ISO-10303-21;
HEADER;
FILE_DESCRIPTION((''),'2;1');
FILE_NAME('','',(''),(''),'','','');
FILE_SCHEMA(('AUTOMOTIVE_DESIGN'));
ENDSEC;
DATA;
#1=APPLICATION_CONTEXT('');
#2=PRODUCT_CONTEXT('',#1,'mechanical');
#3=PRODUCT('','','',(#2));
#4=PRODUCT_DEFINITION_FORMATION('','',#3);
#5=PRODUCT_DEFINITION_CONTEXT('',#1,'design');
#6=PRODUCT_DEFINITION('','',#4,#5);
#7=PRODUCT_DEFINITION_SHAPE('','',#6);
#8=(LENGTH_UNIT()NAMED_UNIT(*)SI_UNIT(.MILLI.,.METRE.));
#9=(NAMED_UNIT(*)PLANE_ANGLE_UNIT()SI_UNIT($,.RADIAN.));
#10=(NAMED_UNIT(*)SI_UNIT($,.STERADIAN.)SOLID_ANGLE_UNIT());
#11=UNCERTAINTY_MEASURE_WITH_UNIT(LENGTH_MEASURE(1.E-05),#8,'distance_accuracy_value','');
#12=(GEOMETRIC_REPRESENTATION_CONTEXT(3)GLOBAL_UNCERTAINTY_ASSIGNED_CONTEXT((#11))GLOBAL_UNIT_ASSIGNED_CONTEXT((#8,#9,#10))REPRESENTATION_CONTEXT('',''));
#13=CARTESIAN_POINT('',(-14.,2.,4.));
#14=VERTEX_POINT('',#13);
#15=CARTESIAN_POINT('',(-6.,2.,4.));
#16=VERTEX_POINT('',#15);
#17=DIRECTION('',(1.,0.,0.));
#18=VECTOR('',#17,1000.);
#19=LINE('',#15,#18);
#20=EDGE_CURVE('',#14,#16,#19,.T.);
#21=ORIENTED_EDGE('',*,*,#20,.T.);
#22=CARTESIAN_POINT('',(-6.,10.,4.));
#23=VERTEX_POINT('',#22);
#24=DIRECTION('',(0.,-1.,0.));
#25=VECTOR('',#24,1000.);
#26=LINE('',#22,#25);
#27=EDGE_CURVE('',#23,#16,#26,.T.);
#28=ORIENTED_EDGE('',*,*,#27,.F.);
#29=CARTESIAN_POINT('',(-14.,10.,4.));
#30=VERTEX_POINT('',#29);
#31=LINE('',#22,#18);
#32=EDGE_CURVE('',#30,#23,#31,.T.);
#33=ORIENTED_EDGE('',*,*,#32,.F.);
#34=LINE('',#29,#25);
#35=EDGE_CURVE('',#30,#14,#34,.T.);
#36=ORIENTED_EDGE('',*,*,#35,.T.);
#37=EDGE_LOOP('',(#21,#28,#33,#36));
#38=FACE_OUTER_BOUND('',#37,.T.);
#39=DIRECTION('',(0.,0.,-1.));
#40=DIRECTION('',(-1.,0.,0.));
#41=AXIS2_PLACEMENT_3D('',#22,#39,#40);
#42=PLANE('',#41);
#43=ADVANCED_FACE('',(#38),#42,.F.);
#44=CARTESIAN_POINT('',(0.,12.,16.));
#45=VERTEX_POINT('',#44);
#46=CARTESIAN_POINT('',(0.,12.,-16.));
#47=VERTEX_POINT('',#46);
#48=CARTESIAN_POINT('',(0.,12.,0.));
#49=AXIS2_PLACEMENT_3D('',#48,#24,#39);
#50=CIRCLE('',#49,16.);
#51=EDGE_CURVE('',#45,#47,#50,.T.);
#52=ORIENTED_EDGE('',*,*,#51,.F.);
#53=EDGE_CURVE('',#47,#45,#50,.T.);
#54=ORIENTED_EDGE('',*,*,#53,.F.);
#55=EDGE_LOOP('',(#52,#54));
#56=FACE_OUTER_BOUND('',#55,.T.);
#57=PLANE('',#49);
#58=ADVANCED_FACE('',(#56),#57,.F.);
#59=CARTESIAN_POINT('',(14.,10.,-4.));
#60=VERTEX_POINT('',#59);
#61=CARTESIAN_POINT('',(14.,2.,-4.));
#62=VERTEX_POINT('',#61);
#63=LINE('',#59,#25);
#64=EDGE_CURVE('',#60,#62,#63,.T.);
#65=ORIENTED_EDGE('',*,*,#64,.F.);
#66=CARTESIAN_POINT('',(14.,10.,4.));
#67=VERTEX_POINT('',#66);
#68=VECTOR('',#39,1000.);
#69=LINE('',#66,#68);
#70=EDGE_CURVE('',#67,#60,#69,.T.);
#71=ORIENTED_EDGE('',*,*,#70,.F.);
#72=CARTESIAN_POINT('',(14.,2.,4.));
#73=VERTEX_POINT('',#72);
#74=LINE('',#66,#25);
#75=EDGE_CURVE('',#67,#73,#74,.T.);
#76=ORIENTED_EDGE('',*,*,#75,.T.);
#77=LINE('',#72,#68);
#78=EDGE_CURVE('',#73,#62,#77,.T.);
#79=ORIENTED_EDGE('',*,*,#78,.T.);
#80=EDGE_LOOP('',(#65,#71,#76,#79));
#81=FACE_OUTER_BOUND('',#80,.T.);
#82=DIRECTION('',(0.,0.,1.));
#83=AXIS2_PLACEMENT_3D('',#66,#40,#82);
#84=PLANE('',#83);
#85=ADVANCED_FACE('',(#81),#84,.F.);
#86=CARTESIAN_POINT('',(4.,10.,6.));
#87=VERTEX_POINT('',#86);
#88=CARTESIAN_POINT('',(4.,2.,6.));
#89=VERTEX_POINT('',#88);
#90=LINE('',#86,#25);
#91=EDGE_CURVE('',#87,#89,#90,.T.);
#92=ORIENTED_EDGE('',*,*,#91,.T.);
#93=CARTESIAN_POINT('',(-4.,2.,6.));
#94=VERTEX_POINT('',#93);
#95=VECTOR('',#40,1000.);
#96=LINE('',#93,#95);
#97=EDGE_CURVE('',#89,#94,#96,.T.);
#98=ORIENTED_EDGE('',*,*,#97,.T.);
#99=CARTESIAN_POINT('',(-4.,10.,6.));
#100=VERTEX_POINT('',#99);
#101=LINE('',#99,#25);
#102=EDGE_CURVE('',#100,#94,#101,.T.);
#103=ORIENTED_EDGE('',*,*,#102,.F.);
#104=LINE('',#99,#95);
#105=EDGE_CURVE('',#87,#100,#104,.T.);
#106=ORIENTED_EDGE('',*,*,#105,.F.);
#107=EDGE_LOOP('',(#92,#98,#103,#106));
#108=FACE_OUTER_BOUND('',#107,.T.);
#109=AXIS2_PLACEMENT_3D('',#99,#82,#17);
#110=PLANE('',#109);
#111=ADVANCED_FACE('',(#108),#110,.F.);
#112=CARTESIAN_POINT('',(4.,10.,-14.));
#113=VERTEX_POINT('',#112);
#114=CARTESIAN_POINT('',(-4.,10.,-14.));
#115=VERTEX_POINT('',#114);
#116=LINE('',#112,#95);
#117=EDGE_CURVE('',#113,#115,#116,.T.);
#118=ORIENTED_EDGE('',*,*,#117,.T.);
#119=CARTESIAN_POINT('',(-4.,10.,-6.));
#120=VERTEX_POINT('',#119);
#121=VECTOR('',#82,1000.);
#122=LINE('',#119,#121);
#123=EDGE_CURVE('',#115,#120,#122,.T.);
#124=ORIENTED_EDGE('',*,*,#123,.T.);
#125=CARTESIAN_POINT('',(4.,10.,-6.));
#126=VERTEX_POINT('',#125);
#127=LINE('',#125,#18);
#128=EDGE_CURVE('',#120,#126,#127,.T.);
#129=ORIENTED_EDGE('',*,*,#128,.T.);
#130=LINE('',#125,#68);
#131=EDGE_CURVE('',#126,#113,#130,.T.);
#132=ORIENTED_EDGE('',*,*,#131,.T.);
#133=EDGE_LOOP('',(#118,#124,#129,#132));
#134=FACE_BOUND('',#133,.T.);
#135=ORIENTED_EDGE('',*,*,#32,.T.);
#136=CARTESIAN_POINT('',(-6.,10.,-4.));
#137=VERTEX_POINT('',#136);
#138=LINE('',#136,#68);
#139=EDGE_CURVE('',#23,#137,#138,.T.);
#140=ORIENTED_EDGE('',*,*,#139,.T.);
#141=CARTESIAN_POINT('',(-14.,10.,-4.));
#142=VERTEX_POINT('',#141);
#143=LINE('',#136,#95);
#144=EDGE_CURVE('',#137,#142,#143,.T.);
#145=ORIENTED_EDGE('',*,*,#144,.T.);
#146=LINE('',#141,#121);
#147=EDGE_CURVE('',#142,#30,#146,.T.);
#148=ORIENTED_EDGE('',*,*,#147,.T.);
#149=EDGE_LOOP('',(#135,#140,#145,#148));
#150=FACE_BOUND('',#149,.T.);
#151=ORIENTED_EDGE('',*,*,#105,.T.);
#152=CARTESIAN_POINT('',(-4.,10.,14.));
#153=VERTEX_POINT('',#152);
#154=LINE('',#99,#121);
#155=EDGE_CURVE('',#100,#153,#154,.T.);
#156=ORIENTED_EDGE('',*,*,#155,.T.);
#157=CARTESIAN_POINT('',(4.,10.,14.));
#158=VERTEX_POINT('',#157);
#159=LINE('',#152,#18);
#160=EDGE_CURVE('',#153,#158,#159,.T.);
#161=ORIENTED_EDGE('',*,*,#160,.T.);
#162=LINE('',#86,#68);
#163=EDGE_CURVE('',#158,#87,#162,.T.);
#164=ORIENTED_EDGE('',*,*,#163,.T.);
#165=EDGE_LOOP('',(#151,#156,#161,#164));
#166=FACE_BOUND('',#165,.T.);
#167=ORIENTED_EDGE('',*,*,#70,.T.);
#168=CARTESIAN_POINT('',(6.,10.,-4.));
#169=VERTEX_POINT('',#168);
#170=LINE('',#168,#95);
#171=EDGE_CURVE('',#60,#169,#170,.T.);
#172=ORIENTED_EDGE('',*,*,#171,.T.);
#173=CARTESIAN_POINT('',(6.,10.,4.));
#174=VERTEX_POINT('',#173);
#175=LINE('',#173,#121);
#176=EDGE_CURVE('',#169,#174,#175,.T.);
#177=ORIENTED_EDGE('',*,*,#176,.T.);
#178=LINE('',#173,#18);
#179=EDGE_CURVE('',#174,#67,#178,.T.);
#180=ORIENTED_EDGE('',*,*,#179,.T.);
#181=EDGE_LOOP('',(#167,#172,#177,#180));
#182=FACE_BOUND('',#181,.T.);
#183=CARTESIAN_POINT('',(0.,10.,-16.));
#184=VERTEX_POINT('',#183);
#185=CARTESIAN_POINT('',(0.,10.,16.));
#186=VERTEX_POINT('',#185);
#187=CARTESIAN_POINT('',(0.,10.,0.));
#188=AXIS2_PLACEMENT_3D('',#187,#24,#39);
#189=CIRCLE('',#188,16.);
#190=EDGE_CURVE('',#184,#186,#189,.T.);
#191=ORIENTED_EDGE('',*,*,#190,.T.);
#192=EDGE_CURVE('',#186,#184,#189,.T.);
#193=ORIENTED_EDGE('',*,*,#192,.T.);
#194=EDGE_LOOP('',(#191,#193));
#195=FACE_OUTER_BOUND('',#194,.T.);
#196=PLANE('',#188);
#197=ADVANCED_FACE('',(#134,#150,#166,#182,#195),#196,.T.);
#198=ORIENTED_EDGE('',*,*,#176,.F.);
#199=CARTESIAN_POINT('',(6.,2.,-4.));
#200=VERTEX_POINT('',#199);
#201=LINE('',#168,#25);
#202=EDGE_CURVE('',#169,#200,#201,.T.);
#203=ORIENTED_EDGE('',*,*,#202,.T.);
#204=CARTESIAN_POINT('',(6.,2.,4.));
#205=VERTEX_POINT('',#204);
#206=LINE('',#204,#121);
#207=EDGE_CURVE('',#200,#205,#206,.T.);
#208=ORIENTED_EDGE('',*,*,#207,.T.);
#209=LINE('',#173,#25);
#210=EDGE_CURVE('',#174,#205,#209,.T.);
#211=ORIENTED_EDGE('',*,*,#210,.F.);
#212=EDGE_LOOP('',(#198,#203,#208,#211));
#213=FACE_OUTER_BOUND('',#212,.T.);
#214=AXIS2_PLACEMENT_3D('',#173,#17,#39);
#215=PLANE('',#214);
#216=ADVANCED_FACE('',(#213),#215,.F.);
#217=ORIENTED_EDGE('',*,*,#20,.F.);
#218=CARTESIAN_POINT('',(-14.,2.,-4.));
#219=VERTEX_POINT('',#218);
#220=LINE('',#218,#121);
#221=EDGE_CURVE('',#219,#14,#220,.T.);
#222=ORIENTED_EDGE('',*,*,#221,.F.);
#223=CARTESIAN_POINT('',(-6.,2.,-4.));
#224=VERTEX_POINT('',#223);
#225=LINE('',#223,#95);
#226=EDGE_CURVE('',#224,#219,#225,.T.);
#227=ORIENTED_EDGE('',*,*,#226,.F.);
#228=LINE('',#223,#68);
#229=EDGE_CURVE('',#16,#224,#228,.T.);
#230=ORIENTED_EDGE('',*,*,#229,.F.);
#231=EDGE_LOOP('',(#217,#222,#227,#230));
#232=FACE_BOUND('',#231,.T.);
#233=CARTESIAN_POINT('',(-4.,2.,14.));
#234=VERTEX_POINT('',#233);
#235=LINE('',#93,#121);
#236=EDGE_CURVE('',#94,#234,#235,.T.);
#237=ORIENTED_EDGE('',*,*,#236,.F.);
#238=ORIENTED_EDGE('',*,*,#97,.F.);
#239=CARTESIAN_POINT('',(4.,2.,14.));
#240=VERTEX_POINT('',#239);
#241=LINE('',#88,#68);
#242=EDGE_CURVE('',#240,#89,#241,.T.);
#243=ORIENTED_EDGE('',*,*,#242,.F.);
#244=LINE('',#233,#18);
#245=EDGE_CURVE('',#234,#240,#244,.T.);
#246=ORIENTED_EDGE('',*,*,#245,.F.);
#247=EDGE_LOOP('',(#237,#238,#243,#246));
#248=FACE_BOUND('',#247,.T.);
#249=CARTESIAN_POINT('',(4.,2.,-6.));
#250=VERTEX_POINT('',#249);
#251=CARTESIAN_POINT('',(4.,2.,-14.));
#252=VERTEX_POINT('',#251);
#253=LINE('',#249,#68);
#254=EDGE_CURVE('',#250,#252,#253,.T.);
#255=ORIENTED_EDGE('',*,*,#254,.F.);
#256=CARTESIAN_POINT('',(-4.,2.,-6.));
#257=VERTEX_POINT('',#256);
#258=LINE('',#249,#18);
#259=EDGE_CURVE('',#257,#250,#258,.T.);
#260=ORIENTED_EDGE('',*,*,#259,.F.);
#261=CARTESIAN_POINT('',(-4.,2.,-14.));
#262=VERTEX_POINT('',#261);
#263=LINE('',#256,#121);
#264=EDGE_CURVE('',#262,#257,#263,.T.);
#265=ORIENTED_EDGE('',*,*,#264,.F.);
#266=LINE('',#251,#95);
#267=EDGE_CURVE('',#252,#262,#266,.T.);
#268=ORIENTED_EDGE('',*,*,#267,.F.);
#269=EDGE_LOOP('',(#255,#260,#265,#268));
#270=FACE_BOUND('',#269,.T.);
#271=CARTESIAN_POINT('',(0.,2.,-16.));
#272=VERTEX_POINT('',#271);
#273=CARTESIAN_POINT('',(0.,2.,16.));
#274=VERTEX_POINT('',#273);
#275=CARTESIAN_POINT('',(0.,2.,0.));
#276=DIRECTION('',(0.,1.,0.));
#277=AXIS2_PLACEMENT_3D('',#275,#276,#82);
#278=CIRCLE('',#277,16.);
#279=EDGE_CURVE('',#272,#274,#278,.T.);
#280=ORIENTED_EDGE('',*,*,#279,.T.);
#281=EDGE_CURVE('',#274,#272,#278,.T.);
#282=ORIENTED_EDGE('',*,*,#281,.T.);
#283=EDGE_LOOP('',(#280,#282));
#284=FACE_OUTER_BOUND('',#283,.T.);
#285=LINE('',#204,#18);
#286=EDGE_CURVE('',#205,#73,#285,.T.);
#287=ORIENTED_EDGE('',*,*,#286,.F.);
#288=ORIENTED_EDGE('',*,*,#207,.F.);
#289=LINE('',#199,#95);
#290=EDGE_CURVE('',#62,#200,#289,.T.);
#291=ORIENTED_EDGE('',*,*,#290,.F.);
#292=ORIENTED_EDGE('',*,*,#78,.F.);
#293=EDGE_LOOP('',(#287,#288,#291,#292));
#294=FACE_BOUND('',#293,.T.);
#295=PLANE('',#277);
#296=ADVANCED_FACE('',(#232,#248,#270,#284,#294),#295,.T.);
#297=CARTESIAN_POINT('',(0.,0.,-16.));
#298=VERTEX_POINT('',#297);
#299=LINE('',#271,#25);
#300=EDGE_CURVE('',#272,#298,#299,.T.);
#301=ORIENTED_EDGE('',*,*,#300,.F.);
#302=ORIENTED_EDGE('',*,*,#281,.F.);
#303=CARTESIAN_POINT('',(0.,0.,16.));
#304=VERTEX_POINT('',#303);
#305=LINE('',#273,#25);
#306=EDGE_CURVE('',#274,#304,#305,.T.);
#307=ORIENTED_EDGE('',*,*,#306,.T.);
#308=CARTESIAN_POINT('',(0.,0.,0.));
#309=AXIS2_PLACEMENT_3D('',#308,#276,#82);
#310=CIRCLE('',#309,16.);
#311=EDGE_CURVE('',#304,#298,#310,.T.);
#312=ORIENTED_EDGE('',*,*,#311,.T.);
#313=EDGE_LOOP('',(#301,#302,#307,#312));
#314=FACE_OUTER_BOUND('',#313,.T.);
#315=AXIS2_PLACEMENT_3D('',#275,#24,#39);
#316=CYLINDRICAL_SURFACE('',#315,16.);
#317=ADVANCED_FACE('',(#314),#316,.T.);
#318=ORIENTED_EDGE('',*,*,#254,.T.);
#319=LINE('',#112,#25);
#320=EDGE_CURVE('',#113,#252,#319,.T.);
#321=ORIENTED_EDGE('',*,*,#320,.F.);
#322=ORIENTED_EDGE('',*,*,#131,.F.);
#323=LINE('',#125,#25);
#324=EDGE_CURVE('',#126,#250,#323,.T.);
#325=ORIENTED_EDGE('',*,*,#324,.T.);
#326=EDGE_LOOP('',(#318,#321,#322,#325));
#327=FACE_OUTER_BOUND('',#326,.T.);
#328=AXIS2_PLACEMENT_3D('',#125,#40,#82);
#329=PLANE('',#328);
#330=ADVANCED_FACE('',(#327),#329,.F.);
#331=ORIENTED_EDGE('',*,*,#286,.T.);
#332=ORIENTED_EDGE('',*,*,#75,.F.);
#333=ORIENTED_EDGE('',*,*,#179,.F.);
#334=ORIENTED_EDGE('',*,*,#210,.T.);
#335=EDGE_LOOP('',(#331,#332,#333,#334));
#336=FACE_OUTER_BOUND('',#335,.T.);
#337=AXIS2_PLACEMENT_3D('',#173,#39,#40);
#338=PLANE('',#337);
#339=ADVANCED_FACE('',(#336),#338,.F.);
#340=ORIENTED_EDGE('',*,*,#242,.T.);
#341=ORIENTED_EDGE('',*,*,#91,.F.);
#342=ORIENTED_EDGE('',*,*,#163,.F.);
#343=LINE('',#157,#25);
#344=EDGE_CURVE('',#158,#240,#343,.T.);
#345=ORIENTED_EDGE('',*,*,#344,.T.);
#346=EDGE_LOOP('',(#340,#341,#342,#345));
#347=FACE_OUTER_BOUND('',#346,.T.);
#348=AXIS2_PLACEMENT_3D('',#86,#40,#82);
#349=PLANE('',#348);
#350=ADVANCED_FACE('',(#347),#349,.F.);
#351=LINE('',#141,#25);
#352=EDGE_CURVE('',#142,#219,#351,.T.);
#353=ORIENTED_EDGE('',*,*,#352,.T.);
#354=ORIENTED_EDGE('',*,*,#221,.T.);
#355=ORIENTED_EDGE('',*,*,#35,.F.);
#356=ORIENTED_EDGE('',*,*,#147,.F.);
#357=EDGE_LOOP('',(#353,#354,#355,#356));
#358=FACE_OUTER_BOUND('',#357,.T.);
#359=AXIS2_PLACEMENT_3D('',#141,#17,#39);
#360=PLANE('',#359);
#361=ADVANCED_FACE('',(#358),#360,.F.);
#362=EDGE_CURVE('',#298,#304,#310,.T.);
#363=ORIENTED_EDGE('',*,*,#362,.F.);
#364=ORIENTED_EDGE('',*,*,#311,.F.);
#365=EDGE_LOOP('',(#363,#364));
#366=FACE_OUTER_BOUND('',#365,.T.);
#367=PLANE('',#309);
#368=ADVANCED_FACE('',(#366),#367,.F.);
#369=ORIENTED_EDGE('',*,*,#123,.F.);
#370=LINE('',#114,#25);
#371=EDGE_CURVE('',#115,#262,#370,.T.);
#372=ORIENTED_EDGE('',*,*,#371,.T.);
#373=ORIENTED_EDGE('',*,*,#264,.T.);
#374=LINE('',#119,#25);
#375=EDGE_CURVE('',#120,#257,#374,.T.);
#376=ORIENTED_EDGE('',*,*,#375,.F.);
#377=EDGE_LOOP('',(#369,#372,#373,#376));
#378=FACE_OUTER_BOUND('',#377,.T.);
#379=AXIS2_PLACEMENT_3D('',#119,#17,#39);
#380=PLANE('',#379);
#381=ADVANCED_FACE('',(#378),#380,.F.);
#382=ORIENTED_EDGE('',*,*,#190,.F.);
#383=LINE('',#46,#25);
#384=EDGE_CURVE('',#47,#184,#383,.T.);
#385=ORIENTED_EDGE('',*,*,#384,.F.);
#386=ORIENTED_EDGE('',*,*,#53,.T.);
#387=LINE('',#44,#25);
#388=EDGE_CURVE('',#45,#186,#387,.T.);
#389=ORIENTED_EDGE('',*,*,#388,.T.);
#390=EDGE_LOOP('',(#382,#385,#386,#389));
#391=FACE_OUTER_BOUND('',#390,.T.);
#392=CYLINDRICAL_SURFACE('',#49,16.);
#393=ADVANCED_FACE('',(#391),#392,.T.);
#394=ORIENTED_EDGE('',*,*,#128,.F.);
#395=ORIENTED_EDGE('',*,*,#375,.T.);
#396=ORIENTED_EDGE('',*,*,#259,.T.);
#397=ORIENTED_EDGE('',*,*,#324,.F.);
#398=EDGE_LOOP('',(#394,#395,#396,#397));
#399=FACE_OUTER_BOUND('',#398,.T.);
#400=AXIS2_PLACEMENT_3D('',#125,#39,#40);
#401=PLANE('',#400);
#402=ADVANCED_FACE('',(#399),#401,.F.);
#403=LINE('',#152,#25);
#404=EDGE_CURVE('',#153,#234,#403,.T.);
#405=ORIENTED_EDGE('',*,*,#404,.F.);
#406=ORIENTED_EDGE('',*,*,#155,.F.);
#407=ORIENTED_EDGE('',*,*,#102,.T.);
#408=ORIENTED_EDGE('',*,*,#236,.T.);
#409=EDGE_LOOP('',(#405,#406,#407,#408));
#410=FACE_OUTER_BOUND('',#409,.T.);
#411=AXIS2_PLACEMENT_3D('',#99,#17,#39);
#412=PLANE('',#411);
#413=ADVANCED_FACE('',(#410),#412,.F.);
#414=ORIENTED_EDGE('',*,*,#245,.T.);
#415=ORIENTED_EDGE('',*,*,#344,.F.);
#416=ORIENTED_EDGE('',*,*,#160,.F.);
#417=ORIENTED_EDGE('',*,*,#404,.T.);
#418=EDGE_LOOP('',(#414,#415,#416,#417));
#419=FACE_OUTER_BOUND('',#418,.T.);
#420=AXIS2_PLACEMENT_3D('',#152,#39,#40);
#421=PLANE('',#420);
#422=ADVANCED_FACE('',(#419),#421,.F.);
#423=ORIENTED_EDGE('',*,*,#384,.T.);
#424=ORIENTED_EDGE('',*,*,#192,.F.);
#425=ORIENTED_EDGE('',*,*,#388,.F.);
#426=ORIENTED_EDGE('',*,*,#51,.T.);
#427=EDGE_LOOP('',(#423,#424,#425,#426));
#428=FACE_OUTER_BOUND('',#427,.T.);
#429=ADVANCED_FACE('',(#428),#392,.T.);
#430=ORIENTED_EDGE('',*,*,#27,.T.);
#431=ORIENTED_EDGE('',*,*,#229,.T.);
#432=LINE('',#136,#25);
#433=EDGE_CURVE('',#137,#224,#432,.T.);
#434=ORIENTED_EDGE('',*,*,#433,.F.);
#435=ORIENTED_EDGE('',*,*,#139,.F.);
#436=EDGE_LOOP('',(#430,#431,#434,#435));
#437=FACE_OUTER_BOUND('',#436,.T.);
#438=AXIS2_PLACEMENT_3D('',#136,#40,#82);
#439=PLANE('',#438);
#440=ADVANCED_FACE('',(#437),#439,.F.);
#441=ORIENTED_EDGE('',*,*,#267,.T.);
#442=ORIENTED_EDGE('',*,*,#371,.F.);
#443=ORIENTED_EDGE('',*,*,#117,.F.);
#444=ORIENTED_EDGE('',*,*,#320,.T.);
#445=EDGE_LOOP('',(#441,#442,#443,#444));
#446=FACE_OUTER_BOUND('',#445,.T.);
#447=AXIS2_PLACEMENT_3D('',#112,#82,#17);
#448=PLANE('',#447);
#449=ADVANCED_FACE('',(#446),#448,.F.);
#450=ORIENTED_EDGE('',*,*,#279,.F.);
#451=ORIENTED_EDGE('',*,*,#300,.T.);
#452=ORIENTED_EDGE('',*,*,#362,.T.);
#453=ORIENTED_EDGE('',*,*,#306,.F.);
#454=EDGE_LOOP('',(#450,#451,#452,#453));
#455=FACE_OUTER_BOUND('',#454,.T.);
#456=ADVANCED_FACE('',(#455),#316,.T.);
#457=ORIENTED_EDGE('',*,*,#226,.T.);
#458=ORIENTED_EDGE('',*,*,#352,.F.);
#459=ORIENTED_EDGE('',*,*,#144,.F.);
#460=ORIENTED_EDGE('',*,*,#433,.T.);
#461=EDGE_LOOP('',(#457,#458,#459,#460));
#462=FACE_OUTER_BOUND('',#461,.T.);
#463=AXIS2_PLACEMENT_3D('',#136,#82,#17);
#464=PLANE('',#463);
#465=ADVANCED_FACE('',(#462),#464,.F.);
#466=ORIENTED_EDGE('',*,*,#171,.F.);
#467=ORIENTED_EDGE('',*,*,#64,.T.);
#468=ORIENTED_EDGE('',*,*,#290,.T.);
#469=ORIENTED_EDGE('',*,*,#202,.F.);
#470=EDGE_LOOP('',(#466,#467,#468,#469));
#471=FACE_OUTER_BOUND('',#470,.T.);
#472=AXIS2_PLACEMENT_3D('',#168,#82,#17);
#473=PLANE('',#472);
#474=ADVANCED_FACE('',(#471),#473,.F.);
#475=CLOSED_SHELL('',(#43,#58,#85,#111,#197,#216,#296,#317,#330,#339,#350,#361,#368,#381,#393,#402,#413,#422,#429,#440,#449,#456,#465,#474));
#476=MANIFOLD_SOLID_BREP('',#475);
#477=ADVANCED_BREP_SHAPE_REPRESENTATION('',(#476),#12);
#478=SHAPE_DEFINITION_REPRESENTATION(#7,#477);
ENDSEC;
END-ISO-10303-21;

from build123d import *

# Parameters (mm, degrees)
SKETCH1_R           = 16
BOSS_EXTRUDE2_DEPTH = 2
SKETCH4_W           = 8
SKETCH4_H           = 8
BOSS_EXTRUDE7_DEPTH = 8
SKETCH5_R           = 16
BOSS_EXTRUDE8_DEPTH = 2


with BuildPart() as part:
    # Sketch1 → Boss-Extrude2 (new body)
    with BuildSketch(Plane(origin=(0, 0, 0), x_dir=(1, 0, 0), z_dir=(0, 1, 0))):
        with Locations(Location((0, 0, 0), (0, 0, 270))):
            Circle(SKETCH1_R)
    extrude(amount=BOSS_EXTRUDE2_DEPTH)

    # Sketch4 → Boss-Extrude7 (add)
    with BuildSketch(Plane(origin=(0, 2, 0), x_dir=(1, 0, 0), z_dir=(0, 1, 0))):
        with Locations((-10, 0)):
            Rectangle(SKETCH4_W, SKETCH4_H)
        with Locations((0, -10)):
            Rectangle(SKETCH4_W, SKETCH4_H)
        with Locations((0, 10)):
            Rectangle(SKETCH4_W, SKETCH4_H)
        with Locations((10, 0)):
            Rectangle(SKETCH4_W, SKETCH4_H)
    extrude(amount=BOSS_EXTRUDE7_DEPTH)

    # Sketch5 → Boss-Extrude8 (add)
    with BuildSketch(Plane(origin=(0, 10, 0), x_dir=(-1, 0, 0), z_dir=(0, -1, 0))):
        with Locations(Location((0, 0, 0), (0, 0, 270))):
            Circle(SKETCH5_R)
    extrude(amount=-BOSS_EXTRUDE8_DEPTH)


solid = part.part
